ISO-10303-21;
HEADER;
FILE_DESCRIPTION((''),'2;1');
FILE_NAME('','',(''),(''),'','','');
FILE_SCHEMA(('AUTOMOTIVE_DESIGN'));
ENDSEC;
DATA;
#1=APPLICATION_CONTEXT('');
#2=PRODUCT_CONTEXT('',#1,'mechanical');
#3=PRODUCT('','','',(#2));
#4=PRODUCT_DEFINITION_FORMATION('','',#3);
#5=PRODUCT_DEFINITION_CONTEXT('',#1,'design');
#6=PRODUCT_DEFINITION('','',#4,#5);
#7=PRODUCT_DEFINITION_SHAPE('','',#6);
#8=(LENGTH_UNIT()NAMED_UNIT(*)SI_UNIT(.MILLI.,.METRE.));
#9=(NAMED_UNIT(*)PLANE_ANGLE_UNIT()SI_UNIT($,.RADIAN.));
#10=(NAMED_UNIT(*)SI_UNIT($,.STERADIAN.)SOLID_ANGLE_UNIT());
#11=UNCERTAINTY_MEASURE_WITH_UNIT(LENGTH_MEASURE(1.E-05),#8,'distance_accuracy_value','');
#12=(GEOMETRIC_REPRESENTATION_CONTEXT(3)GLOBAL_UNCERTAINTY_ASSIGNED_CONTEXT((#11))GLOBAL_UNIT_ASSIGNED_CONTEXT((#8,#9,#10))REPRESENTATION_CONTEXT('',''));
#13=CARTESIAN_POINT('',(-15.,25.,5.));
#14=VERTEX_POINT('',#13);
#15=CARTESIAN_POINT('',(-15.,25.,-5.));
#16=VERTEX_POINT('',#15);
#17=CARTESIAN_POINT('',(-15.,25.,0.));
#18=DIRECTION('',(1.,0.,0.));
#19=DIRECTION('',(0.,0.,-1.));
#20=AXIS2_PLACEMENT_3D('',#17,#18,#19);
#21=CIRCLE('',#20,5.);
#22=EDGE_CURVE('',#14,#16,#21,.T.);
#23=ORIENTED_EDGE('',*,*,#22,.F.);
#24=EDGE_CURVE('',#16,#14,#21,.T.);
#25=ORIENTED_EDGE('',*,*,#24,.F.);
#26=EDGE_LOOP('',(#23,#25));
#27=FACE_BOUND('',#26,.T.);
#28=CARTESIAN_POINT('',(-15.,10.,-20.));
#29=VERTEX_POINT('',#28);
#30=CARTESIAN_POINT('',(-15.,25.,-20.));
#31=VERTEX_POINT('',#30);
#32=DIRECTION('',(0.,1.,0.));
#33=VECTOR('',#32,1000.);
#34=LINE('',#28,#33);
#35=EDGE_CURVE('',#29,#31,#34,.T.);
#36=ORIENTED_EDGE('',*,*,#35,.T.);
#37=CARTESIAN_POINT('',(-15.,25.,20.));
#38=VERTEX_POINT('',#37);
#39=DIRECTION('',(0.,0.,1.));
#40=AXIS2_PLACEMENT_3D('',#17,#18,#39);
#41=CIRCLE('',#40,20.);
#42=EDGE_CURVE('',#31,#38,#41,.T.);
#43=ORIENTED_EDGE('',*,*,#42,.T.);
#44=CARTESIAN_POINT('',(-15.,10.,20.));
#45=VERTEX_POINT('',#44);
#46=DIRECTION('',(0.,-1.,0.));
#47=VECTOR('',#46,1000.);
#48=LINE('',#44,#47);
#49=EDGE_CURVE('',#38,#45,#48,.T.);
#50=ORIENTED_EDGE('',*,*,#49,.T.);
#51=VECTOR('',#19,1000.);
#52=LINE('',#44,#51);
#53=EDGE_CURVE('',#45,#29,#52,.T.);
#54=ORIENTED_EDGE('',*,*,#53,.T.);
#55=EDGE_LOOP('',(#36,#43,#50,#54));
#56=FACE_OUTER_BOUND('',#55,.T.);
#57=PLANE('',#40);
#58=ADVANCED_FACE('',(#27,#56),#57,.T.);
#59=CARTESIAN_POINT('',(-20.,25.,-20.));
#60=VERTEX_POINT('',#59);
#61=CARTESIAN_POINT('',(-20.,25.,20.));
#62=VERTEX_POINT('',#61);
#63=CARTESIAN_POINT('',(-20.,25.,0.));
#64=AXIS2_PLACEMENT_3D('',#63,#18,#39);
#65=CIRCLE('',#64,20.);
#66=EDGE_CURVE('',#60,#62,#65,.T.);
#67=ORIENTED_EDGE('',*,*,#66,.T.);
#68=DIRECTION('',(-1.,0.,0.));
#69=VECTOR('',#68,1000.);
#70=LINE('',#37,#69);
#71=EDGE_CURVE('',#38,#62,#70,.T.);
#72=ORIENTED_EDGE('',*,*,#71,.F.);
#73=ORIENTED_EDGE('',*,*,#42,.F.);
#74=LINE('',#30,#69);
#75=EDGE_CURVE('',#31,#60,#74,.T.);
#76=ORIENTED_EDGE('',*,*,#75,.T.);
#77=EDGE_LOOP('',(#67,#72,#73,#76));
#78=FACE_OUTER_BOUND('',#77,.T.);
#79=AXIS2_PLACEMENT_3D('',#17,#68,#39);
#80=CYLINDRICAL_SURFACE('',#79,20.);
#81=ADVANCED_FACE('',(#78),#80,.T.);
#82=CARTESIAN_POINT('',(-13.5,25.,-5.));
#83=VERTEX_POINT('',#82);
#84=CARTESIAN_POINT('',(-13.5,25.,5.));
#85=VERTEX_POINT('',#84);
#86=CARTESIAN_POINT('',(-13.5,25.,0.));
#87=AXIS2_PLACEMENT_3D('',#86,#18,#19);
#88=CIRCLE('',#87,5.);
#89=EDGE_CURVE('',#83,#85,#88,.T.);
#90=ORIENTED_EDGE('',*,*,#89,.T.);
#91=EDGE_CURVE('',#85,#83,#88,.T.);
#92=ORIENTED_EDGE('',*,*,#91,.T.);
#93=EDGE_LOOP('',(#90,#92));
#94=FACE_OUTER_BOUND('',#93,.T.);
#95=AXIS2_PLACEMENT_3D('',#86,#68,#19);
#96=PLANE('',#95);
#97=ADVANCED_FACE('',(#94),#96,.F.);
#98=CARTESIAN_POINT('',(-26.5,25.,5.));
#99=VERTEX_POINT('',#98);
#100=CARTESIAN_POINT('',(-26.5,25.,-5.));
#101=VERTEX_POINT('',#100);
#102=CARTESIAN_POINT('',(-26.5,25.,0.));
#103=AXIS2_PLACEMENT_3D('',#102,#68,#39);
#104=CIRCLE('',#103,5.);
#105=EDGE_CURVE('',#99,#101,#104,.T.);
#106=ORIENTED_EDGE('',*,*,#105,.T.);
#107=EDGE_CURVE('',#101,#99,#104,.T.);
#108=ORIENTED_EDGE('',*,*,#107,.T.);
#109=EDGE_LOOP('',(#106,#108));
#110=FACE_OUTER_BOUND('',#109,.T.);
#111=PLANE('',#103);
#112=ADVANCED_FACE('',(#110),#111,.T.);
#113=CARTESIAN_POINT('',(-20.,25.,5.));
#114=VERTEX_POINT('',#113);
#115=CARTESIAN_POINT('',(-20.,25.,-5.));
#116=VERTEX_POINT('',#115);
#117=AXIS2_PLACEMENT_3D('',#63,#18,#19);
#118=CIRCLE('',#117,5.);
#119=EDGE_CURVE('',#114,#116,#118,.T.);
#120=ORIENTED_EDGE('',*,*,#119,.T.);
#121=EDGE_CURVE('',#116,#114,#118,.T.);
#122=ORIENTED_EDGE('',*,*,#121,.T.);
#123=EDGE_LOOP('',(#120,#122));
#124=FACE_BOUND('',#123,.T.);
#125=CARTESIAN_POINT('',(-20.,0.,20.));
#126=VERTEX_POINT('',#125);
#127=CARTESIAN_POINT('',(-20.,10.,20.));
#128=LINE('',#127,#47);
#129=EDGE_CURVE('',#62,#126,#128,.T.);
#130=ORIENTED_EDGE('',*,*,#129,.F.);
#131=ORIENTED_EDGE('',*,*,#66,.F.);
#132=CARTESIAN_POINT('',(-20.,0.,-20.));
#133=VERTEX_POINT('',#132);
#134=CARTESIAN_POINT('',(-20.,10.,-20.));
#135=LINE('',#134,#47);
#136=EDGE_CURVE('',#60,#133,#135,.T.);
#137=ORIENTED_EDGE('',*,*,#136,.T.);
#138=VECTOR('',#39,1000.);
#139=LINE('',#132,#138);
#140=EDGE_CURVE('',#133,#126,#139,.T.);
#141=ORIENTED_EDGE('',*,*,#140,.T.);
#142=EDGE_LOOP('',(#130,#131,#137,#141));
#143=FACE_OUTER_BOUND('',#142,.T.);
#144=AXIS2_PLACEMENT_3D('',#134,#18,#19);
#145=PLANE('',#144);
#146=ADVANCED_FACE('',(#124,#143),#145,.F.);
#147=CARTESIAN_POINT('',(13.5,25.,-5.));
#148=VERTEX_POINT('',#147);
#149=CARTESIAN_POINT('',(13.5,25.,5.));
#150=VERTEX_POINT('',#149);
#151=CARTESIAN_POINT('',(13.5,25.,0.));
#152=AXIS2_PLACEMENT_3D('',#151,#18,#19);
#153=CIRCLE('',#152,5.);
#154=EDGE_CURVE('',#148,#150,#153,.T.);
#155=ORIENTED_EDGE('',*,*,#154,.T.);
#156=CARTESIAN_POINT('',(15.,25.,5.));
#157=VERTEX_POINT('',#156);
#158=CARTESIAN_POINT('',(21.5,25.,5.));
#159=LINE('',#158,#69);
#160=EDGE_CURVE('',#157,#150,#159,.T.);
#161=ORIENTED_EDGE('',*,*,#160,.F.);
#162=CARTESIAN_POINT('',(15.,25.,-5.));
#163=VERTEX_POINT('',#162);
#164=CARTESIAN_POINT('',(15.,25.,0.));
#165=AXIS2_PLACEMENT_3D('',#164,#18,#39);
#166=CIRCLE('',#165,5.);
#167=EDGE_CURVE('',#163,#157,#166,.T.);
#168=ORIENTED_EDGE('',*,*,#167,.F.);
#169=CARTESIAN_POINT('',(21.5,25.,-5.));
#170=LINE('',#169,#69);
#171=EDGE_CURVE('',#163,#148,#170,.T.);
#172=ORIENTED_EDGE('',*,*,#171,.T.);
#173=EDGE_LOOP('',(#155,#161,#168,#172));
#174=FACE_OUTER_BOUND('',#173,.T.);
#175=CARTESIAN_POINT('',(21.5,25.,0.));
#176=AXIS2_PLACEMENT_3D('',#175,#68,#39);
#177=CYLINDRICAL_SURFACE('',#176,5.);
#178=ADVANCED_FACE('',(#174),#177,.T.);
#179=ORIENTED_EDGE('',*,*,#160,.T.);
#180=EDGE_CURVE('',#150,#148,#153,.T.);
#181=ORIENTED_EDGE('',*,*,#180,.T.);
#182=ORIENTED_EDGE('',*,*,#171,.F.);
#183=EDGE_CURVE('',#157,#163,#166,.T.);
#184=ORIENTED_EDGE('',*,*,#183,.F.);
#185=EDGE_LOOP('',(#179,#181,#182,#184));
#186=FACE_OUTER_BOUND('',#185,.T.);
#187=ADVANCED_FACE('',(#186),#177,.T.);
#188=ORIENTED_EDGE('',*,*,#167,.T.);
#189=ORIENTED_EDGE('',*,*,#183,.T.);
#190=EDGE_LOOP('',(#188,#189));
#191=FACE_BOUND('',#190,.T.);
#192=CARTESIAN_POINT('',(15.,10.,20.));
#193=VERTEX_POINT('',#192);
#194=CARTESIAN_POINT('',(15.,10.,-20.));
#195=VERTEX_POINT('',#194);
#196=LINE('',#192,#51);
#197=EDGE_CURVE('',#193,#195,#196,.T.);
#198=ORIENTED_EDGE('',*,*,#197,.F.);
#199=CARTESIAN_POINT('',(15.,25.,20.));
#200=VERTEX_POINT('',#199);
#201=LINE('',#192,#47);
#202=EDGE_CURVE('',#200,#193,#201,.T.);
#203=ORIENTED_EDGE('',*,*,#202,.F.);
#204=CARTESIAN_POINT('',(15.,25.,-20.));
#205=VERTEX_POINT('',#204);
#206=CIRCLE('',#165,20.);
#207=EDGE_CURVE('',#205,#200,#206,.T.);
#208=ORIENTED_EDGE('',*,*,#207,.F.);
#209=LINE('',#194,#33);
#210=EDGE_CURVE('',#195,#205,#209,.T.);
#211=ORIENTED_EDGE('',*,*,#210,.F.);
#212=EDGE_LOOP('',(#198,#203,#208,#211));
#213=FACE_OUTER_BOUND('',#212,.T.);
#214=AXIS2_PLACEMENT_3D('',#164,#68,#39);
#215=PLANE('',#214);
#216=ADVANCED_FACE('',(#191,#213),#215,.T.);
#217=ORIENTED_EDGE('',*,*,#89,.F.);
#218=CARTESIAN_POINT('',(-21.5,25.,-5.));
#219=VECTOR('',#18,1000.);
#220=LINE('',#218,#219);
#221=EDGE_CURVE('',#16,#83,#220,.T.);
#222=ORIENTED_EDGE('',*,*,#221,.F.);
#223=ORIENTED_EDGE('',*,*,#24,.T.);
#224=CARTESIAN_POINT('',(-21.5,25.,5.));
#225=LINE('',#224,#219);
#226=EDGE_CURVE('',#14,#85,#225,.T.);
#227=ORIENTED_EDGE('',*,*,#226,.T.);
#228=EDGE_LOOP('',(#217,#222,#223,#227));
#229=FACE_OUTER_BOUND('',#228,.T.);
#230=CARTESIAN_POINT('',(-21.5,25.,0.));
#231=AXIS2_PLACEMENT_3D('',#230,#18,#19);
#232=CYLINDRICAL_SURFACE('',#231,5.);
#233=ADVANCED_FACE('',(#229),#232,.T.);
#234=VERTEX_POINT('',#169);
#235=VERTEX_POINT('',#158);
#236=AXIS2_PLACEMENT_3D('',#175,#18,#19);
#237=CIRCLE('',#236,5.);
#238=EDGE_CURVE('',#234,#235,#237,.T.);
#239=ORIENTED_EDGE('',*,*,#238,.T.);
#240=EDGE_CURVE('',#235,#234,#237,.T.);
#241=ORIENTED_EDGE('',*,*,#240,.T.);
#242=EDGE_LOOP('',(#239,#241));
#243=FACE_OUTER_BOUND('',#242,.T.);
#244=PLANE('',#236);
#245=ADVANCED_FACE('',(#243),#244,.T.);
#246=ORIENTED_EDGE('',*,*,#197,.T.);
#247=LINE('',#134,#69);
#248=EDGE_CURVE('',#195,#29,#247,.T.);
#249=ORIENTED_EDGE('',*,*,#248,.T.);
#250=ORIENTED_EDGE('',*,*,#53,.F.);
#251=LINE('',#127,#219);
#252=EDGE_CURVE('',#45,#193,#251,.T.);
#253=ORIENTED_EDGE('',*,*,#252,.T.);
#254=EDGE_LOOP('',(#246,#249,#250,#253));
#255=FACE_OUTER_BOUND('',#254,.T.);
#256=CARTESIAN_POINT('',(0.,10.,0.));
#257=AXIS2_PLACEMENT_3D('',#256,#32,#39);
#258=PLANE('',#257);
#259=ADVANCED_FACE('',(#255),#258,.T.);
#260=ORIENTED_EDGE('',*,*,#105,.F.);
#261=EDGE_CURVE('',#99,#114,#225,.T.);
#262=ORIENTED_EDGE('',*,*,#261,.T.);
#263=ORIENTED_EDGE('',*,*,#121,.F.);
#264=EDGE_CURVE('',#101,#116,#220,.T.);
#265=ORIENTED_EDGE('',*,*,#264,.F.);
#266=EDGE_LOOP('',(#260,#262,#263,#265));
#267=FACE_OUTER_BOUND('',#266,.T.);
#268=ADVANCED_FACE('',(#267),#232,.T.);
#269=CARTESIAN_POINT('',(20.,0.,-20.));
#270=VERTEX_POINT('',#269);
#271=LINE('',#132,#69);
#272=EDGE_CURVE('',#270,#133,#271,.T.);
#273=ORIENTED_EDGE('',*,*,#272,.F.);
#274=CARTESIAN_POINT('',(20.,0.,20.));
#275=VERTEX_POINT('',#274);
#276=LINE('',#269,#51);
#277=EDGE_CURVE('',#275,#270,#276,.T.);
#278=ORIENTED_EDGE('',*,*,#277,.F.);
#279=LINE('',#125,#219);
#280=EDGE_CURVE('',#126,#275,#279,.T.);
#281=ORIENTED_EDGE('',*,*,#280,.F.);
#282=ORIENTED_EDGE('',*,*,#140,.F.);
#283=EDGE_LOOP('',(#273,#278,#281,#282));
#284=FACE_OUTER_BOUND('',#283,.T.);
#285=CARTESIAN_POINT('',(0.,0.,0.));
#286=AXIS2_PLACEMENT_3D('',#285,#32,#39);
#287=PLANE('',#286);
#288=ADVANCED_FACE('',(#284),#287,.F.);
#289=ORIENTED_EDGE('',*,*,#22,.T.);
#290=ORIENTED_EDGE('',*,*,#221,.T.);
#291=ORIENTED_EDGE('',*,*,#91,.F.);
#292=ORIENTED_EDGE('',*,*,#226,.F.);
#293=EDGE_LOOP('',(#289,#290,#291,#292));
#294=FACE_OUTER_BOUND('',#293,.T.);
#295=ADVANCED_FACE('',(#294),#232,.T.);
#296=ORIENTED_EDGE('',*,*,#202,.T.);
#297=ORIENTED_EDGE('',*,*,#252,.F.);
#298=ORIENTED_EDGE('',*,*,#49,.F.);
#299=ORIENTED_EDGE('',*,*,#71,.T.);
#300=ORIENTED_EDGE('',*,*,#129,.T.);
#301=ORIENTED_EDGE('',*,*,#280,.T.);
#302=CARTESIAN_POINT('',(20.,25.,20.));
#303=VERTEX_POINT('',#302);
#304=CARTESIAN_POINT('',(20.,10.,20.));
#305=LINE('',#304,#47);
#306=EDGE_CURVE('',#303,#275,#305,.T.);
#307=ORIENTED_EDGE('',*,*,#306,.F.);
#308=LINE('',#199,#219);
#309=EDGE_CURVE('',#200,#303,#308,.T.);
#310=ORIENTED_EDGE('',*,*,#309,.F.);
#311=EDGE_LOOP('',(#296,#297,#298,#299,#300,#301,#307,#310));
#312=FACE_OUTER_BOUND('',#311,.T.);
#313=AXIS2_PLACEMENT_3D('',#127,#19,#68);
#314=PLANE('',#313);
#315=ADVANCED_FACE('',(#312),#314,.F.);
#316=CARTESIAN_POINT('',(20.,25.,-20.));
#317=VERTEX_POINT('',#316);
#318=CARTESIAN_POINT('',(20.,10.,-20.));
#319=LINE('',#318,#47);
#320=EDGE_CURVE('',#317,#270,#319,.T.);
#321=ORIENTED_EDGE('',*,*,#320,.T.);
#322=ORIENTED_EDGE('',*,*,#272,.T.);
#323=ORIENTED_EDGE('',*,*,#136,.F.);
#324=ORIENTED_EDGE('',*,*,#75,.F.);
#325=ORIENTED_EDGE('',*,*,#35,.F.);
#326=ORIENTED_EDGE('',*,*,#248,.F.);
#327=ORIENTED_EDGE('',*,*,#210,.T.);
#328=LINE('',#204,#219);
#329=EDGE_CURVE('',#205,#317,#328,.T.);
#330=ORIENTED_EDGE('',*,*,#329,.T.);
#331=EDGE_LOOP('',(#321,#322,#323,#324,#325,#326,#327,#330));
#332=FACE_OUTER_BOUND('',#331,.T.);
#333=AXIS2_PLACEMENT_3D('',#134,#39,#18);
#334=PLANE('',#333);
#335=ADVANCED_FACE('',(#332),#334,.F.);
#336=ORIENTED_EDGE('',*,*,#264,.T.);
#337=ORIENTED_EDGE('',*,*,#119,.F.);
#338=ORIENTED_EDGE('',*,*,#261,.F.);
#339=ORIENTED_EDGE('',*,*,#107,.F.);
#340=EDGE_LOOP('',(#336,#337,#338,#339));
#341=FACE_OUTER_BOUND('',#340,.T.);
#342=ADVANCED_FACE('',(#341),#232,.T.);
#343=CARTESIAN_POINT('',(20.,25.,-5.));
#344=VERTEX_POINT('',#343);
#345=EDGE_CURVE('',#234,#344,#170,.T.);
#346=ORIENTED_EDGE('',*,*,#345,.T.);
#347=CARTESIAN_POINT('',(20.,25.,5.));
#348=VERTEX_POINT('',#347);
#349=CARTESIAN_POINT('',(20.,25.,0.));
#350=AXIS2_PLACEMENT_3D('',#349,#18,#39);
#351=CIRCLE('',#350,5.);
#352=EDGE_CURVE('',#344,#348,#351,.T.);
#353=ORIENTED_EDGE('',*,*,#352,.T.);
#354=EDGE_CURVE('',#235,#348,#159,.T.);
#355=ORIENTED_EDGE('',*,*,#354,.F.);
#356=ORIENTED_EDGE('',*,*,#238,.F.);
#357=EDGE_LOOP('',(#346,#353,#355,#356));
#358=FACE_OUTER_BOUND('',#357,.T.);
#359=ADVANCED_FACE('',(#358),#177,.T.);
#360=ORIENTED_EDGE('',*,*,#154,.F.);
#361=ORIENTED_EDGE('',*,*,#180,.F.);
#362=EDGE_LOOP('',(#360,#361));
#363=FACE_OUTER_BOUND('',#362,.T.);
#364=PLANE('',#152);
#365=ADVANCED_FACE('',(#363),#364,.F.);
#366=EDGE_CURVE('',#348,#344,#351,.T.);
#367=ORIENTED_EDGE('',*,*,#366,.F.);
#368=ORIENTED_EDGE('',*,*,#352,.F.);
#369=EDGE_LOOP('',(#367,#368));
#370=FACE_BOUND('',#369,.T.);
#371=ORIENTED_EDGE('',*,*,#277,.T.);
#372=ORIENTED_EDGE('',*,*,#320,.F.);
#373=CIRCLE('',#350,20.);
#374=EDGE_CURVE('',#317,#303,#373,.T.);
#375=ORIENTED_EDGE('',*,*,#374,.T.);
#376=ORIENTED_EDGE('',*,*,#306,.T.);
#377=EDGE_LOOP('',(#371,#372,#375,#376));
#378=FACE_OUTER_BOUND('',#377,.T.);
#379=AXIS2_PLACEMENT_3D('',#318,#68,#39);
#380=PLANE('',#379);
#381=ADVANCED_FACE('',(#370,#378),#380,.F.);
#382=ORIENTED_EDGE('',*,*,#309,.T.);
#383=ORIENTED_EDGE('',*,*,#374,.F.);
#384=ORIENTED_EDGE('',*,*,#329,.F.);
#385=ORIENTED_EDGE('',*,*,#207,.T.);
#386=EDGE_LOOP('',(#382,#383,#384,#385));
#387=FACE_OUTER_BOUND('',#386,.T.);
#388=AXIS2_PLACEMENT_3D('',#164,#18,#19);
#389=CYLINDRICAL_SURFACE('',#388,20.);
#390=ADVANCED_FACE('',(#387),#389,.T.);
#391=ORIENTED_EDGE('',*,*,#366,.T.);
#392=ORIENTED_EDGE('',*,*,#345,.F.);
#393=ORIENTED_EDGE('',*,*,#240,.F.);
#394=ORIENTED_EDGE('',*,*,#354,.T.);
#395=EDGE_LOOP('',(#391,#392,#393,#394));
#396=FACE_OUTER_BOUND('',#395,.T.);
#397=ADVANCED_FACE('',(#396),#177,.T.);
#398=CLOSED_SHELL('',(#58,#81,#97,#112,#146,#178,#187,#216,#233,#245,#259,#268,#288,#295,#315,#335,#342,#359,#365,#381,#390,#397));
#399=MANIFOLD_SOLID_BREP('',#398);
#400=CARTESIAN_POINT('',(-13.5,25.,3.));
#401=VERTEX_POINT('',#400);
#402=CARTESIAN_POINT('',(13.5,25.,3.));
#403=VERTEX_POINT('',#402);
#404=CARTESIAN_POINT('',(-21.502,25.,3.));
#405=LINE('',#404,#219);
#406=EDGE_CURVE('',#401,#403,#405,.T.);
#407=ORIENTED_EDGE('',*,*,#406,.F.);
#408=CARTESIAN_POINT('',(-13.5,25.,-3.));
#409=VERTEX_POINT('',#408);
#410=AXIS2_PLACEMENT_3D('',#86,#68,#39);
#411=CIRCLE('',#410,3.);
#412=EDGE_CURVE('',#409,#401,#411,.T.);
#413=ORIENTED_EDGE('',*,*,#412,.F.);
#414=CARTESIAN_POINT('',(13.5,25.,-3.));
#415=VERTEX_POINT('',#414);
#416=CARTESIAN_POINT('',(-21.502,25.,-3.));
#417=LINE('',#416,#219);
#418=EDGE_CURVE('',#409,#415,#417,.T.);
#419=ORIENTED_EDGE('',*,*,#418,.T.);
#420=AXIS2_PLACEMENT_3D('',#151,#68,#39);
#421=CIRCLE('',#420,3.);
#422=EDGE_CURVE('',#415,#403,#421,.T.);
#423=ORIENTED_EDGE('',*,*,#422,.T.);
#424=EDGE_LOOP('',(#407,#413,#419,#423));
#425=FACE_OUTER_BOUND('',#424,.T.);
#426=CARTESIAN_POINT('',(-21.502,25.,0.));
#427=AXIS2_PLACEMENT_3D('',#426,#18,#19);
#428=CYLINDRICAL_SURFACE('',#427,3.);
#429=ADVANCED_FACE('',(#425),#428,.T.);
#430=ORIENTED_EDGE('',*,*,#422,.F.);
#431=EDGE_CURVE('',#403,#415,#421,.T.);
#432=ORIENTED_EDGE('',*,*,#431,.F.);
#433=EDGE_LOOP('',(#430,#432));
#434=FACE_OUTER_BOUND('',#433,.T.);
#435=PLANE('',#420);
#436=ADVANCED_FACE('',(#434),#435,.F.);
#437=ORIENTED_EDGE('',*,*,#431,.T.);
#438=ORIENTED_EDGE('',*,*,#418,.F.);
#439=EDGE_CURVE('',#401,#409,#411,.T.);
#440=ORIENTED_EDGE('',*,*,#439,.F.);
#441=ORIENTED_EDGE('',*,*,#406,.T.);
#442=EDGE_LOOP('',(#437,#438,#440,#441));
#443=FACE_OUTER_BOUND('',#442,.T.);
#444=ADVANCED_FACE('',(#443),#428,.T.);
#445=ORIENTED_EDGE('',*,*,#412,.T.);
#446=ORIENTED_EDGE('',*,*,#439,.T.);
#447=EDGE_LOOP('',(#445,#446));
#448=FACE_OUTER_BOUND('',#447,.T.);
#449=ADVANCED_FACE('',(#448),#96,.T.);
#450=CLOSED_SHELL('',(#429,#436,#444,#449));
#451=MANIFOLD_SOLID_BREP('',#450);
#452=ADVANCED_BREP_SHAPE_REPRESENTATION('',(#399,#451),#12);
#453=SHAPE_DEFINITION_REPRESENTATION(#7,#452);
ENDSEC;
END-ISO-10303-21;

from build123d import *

# Parameters (mm, degrees)
SKETCH1_W           = 40
SKETCH1_H           = 40
BOSS_EXTRUDE1_DEPTH = 10
BOSS_EXTRUDE2_DEPTH = 5
SKETCH4_R           = 5
BOSS_EXTRUDE3_DEPTH = 4
BOSS_EXTRUDE4_REACH = 62.415
SKETCH5_R           = 3
SKETCH6_R           = 5
BOSS_EXTRUDE5_DEPTH = 5


with BuildPart() as part:
    # Sketch1 → Boss-Extrude1 (new body)
    with BuildSketch(Plane(origin=(0, 0, 0), x_dir=(1, 0, 0), z_dir=(0, 1, 0))):
        Rectangle(SKETCH1_W, SKETCH1_H)
    extrude(amount=BOSS_EXTRUDE1_DEPTH)

    # Sketch2 → Boss-Extrude2 (add)
    with BuildSketch(Plane(origin=(20, 0, 0), x_dir=(0, 0, -1), z_dir=(1, 0, 0))):
        with BuildLine():
            Line((-20, 10), (-20, 25))
            ThreePointArc((-20, 25), (0, 45), (20, 25))
            Line((20, 25), (20, 10))
            Line((20, 10), (-20, 10))
        make_face()
    boss_extrude2 = extrude(amount=-BOSS_EXTRUDE2_DEPTH)

    # Mirror1: Boss-Extrude2 across plane
    add(boss_extrude2.mirror(Plane(origin=(0, 0, 0), x_dir=(0, 0, 1), z_dir=(1, 0, 0))))

    # Sketch4 → Boss-Extrude3 (add, symmetric)
    with BuildSketch(Plane(origin=(17.5, 0, 0), x_dir=(0, 0, -1), z_dir=(1, 0, 0))):
        with Locations(Location((0, 25, 0), (0, 0, 180))):
            Circle(SKETCH4_R)
    boss_extrude3 = extrude(amount=BOSS_EXTRUDE3_DEPTH, both=True)

    # Mirror2: Boss-Extrude3 across plane
    add(boss_extrude3.mirror(Plane(origin=(0, 0, 0), x_dir=(0, 0, 1), z_dir=(1, 0, 0))))


with BuildPart() as body_2:

    # Sketch5 → Boss-Extrude4 (new, up to next)
    with BuildSketch(Plane.ZY.offset(-13.5), mode=Mode.PRIVATE) as boss_extrude4_sk1:
        with Locations((0, 25)):
            Circle(SKETCH5_R)
    boss_extrude4_tool1 = extrude(boss_extrude4_sk1.sketch, amount=BOSS_EXTRUDE4_REACH, mode=Mode.PRIVATE) - part.part
    add(boss_extrude4_tool1.solids().sort_by_distance((13.5, 25, 0))[0])


with BuildPart() as part_1:
    add(part.part)

    # Sketch6 → Boss-Extrude5 (add)
    with BuildSketch(Plane.ZY.offset(21.5)):
        with Locations((0, 25)):
            Circle(SKETCH6_R)
    extrude(amount=BOSS_EXTRUDE5_DEPTH)


solid = Compound([body_2.part, part_1.part])
